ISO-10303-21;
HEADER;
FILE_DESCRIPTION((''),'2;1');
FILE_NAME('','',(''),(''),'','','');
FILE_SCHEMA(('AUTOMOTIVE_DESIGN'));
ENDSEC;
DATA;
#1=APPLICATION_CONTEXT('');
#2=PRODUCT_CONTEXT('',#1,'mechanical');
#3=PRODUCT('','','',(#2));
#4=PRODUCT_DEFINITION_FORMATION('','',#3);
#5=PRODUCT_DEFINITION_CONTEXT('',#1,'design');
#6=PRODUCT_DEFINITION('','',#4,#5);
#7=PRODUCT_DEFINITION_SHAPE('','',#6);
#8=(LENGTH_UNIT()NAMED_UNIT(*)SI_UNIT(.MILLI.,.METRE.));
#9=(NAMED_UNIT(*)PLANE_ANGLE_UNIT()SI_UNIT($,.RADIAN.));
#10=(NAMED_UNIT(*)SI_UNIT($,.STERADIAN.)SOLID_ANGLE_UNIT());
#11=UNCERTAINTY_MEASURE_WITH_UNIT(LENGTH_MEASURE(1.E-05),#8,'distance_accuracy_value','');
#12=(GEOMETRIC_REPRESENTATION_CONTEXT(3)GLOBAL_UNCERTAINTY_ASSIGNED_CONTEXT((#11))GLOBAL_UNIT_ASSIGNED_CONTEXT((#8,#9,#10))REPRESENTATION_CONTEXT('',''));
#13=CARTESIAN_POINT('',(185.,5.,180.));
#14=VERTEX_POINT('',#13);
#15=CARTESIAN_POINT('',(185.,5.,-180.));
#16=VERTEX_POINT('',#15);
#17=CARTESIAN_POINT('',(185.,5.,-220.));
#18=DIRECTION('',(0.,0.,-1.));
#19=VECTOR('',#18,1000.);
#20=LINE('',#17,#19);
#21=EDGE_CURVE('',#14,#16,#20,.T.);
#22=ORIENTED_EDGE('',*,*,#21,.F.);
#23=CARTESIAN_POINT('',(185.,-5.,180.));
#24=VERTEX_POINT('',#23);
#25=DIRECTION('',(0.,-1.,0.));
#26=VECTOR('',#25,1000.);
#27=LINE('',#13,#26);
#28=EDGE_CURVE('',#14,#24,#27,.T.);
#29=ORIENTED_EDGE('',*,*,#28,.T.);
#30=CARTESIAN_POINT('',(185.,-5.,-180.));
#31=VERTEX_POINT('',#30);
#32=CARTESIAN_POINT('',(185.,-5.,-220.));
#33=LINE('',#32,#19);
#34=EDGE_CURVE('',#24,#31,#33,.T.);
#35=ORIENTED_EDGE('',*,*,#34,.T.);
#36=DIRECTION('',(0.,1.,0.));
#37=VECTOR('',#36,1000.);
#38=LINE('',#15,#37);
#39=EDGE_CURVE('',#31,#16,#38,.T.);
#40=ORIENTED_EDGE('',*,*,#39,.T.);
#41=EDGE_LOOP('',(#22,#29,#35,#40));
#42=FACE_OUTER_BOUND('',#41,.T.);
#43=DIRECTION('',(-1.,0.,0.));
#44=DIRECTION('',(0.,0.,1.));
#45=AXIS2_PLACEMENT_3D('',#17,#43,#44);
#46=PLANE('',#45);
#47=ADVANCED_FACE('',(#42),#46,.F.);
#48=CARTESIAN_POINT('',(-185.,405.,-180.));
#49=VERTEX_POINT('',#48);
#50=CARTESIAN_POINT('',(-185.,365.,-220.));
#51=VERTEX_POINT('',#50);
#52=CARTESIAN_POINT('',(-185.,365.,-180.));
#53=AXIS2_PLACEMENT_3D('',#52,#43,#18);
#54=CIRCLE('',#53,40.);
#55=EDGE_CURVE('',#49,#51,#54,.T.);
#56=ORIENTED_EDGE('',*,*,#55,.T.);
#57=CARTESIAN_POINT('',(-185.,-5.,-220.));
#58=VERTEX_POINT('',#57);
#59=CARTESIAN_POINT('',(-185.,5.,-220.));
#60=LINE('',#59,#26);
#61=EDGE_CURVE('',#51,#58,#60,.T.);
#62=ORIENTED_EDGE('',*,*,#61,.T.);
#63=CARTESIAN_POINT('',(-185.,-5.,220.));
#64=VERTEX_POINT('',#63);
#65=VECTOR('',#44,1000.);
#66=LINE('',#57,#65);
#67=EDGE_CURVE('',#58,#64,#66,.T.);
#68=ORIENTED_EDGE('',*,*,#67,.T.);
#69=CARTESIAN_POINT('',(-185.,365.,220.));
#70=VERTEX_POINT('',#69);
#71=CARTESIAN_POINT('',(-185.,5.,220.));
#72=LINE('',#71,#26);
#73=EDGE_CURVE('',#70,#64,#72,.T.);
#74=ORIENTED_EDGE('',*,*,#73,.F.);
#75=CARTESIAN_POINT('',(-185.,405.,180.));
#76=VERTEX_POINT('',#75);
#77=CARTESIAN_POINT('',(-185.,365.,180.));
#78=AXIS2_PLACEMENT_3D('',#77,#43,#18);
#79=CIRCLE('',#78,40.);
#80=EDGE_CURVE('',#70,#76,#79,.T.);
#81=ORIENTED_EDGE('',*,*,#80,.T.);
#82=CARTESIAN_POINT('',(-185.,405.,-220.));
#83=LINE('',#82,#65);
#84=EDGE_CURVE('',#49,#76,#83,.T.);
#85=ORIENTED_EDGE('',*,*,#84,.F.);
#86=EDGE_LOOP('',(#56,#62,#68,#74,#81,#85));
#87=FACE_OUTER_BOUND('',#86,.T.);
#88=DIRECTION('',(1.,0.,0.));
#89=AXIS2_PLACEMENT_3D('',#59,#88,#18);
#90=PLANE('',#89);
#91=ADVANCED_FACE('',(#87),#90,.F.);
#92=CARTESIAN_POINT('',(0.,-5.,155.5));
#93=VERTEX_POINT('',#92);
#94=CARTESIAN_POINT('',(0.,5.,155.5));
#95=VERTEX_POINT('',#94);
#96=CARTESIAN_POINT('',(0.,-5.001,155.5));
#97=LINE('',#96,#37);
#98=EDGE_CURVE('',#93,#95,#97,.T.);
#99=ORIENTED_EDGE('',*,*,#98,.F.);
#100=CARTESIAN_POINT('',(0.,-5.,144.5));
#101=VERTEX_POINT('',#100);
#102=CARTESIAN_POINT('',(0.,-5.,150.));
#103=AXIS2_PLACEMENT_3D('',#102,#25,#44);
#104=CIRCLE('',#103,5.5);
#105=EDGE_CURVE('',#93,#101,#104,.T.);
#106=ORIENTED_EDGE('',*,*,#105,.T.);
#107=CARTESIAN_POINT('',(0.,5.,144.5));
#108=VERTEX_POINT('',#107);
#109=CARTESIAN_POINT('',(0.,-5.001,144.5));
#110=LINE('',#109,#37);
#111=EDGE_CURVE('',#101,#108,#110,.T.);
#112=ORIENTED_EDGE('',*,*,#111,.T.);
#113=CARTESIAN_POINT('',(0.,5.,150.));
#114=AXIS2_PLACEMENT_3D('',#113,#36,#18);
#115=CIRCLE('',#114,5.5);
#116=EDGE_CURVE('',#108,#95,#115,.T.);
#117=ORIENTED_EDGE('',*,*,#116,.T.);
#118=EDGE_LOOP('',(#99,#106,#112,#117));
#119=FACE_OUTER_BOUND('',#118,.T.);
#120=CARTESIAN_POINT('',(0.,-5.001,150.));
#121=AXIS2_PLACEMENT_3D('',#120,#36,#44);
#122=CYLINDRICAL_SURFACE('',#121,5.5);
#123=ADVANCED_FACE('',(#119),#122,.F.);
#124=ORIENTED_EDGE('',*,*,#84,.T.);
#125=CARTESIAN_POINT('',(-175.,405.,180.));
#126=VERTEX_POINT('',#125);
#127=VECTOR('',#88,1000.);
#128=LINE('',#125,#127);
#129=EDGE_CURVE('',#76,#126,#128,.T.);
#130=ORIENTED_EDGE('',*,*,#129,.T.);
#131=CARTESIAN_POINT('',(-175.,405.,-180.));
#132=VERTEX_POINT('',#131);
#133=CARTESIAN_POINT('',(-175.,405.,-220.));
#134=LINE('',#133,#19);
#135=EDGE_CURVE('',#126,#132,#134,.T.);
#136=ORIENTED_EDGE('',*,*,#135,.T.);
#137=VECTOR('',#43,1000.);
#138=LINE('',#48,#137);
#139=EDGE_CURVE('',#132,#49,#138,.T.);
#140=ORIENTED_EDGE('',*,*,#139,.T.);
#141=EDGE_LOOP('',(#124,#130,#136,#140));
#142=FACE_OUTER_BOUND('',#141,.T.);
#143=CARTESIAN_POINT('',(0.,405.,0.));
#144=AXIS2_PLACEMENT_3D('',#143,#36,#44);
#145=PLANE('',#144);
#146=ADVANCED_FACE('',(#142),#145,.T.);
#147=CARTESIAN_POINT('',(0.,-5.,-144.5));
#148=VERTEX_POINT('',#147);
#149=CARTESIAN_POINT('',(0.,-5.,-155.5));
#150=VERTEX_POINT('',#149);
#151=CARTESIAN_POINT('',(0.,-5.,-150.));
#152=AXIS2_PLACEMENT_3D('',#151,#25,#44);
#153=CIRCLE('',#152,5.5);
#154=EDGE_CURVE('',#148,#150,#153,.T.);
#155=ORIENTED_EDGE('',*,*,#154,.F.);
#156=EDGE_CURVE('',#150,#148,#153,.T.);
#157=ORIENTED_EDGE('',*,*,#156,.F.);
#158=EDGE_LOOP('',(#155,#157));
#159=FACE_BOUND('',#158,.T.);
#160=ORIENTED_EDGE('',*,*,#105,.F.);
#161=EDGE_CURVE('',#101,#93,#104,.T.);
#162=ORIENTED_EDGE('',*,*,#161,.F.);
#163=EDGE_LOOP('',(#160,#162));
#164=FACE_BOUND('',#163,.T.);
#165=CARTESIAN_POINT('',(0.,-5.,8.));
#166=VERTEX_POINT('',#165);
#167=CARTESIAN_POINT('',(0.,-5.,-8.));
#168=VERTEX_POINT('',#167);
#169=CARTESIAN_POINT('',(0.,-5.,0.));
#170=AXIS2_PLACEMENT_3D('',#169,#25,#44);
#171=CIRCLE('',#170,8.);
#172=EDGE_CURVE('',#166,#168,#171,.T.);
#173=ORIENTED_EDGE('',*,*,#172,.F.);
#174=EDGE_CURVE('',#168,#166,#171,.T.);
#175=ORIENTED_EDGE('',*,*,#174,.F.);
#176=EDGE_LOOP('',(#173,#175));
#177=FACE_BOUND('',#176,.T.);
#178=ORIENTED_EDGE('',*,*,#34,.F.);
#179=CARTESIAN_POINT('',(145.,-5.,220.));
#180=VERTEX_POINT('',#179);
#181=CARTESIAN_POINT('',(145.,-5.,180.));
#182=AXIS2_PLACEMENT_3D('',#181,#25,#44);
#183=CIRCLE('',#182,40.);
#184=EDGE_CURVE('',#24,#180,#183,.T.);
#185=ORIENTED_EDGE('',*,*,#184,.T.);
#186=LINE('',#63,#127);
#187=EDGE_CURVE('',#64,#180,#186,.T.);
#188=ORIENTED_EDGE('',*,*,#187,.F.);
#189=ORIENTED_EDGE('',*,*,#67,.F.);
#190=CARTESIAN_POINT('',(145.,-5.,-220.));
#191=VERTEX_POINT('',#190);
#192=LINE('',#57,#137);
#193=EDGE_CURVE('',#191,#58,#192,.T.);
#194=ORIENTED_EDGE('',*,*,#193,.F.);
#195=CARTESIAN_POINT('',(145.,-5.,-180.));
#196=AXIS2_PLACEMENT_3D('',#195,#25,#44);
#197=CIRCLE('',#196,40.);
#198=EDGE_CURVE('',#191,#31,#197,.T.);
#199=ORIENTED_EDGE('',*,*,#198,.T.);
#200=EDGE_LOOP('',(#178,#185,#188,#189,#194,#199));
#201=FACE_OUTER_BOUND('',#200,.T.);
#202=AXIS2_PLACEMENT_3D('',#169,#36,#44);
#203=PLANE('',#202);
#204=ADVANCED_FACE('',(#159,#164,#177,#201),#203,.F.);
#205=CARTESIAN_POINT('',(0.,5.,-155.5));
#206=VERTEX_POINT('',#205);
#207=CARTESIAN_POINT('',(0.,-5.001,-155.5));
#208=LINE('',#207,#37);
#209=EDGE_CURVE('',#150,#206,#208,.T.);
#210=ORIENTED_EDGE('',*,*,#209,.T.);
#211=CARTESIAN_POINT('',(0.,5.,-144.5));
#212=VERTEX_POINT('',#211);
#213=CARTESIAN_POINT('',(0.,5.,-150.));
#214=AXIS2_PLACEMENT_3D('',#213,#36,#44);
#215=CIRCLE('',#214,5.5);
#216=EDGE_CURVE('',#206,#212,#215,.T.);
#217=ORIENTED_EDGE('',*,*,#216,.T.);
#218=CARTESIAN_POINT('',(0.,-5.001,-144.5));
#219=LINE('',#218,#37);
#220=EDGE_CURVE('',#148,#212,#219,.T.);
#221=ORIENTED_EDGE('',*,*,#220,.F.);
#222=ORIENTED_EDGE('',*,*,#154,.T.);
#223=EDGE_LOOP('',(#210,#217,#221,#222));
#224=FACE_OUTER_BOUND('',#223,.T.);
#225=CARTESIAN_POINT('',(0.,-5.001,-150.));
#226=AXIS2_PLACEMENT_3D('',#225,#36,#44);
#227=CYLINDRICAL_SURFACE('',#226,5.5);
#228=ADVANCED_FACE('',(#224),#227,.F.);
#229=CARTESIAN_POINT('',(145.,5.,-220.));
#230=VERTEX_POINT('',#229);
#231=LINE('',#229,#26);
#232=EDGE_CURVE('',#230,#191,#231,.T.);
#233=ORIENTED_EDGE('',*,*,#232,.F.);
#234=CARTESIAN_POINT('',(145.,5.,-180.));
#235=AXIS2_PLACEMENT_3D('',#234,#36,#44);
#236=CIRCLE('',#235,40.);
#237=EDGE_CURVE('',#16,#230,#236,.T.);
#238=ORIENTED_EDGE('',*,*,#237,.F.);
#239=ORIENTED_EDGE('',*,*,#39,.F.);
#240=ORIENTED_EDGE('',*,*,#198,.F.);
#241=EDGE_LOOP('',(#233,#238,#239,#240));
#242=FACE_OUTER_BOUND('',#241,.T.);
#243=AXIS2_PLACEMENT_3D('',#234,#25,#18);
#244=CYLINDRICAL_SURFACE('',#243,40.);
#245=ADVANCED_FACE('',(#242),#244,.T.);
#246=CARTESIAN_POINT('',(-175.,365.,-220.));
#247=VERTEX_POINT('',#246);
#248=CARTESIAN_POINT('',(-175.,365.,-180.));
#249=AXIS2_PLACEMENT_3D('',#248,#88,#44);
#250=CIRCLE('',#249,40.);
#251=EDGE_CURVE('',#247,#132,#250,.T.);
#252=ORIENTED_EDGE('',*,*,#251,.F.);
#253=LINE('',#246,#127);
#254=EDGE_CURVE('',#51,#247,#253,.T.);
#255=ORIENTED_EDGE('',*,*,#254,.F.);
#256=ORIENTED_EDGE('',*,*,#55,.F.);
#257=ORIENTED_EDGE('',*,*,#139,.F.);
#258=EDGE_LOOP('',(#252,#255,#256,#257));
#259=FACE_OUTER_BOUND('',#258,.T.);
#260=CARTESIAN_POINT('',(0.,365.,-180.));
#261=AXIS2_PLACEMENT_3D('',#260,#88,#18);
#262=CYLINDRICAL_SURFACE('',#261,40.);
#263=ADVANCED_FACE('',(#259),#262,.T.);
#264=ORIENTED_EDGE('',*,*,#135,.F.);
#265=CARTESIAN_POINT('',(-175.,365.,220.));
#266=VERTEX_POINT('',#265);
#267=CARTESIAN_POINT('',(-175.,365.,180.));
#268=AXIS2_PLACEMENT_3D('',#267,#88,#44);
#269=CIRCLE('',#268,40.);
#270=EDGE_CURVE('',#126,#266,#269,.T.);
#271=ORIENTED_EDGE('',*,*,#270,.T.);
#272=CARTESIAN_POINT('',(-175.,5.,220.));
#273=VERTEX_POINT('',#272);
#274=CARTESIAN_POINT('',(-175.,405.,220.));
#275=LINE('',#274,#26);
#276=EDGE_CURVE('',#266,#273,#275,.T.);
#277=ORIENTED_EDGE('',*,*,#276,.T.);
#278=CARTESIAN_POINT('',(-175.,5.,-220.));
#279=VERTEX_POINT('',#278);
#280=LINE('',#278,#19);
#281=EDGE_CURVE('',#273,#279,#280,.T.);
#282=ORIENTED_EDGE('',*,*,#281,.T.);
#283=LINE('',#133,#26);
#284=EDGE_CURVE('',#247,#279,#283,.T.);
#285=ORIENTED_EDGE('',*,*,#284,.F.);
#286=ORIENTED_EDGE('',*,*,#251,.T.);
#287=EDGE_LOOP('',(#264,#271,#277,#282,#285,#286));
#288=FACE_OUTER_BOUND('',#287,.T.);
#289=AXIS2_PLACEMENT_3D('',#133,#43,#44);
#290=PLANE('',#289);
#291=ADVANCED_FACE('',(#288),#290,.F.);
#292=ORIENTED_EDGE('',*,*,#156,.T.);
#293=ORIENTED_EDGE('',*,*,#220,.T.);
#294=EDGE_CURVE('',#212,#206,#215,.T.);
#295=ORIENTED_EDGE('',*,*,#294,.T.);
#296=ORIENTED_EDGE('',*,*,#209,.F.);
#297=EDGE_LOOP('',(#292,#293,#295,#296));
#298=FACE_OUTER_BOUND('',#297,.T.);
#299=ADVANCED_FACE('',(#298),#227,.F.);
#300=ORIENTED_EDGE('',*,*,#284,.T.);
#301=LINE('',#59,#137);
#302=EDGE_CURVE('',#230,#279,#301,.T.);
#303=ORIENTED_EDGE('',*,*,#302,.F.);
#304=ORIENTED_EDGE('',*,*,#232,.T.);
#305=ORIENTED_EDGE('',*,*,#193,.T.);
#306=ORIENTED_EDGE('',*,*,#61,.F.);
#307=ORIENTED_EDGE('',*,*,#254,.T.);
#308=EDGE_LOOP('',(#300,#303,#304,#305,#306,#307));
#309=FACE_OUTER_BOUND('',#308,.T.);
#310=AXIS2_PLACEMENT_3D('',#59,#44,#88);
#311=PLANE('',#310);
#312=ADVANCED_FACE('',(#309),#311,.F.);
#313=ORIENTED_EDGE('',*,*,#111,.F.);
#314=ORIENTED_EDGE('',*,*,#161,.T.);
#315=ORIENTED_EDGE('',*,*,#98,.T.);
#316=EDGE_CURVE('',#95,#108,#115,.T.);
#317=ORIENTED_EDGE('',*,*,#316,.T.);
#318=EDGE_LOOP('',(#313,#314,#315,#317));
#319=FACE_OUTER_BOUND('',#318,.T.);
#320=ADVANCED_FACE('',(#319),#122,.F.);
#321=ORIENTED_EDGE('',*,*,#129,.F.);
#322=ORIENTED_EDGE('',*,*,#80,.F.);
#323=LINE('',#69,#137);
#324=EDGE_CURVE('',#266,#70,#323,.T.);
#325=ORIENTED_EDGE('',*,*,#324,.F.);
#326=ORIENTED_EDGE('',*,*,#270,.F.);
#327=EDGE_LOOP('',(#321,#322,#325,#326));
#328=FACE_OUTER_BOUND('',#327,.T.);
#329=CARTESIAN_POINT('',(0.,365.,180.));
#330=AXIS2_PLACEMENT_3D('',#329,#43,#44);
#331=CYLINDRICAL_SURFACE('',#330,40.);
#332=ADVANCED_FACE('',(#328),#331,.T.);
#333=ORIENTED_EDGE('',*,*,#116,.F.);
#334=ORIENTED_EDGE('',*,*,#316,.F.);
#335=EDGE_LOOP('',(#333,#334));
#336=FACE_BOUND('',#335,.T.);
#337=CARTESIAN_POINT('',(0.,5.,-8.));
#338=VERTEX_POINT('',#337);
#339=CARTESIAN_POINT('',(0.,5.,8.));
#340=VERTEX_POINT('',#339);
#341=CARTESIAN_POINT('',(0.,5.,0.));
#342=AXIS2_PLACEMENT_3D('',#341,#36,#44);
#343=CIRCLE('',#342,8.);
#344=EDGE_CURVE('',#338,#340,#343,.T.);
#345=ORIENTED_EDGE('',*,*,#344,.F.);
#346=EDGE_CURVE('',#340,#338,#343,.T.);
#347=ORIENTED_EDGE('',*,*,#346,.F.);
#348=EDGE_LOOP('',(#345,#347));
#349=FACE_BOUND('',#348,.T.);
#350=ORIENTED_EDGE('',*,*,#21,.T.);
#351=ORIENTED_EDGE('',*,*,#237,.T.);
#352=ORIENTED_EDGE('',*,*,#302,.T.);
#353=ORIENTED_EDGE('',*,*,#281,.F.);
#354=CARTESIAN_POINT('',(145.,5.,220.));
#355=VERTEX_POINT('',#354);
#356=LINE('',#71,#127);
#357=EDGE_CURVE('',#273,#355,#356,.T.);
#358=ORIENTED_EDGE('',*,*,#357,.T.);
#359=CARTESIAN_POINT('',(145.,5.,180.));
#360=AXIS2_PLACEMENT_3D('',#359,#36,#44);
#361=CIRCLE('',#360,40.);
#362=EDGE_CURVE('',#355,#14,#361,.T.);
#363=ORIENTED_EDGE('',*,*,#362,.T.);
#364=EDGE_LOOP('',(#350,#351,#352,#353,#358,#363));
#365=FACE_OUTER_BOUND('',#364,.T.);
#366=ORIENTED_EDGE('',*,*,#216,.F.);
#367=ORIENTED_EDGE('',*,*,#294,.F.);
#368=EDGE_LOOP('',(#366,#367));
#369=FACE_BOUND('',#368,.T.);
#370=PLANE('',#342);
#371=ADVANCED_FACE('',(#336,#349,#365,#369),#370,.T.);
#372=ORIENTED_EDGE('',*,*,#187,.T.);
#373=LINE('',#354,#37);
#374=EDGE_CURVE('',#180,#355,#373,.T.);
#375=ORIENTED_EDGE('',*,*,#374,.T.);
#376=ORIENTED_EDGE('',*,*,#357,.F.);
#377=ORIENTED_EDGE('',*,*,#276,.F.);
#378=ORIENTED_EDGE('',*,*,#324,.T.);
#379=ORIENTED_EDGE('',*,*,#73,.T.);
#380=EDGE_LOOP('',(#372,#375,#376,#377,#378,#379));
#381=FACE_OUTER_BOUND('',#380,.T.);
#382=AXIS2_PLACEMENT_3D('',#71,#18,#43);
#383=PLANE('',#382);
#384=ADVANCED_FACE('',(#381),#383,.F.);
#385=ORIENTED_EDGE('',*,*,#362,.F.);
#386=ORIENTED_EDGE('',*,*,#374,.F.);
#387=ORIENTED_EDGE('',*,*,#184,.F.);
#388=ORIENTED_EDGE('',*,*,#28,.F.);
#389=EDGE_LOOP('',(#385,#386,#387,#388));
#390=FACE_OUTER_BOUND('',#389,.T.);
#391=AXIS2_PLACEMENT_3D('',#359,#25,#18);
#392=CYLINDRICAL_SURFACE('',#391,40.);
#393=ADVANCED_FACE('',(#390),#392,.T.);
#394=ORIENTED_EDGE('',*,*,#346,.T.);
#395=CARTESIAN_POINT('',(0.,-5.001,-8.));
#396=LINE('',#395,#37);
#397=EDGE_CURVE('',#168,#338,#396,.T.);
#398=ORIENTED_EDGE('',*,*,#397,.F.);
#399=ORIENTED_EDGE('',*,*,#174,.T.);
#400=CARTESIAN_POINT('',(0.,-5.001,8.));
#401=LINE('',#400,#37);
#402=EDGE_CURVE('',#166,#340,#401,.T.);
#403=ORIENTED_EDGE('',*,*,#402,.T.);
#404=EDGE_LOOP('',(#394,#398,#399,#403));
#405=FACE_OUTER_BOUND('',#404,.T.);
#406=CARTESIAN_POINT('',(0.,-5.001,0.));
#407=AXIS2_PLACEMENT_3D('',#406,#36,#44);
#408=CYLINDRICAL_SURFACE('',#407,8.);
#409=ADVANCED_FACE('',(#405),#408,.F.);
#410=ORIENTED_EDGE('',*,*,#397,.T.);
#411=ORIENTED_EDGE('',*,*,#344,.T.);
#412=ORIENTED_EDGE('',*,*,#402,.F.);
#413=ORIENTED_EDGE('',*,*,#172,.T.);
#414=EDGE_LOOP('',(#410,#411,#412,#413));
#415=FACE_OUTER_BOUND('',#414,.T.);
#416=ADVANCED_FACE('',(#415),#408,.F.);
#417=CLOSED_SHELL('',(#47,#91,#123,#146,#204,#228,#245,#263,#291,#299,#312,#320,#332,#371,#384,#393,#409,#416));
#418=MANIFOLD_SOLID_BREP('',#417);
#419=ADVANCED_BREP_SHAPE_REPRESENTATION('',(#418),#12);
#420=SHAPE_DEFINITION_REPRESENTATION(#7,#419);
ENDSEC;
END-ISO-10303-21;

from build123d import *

# Parameters (mm, degrees)
SKETCH_1_W          = 370
SKETCH_1_H          = 440
EXTRUDE_1_DEPTH     = 5
CUT_EXTRUDE_1_REACH = 289.62
SKETCH_2_R          = 8
SKETCH_2_R_2        = 5.5
SKETCH_3_W          = 10
SKETCH_3_H          = 440
EXTRUDE_2_DEPTH     = 400
FILLET_1_R          = 40


with BuildPart() as part:
    # 草图1 → 凸台-拉伸1 (new, symmetric)
    with BuildSketch(Plane(origin=(0, 0, 0), x_dir=(1, 0, 0), z_dir=(0, 1, 0))):
        Rectangle(SKETCH_1_W, SKETCH_1_H)
    extrude(amount=EXTRUDE_1_DEPTH, both=True)

    # 草图2 → 切除-拉伸1 (cut, up to next)
    with BuildSketch(Plane(origin=(0, 5, 0), x_dir=(1, 0, 0), z_dir=(0, 1, 0)), mode=Mode.PRIVATE) as cut_extrude_1_sk1:
        with Locations(Location((0, 0, 0), (0, 0, 270))):
            Circle(SKETCH_2_R)
    cut_extrude_1_tool1 = extrude(cut_extrude_1_sk1.sketch, amount=-CUT_EXTRUDE_1_REACH, mode=Mode.PRIVATE) & part.part
    # 草图2 → 切除-拉伸1 (cut, up to next)
    with BuildSketch(Plane(origin=(0, 5, 0), x_dir=(1, 0, 0), z_dir=(0, 1, 0)), mode=Mode.PRIVATE) as cut_extrude_1_sk2:
        with Locations(Location((0, 150, 0), (0, 0, 270))):
            Circle(SKETCH_2_R_2)
    cut_extrude_1_tool2 = extrude(cut_extrude_1_sk2.sketch, amount=-CUT_EXTRUDE_1_REACH, mode=Mode.PRIVATE) & part.part
    # 草图2 → 切除-拉伸1 (cut, up to next)
    with BuildSketch(Plane(origin=(0, 5, 0), x_dir=(1, 0, 0), z_dir=(0, 1, 0)), mode=Mode.PRIVATE) as cut_extrude_1_sk3:
        with Locations(Location((0, -150, 0), (0, 0, 270))):
            Circle(SKETCH_2_R_2)
    cut_extrude_1_tool3 = extrude(cut_extrude_1_sk3.sketch, amount=-CUT_EXTRUDE_1_REACH, mode=Mode.PRIVATE) & part.part
    add(cut_extrude_1_tool1.solids().sort_by_distance((0, 5, 0))[0], mode=Mode.SUBTRACT)
    add(cut_extrude_1_tool2.solids().sort_by_distance((0, 5, -150))[0], mode=Mode.SUBTRACT)
    add(cut_extrude_1_tool3.solids().sort_by_distance((0, 5, 150))[0], mode=Mode.SUBTRACT)

    # 草图3 → 凸台-拉伸2 (add)
    with BuildSketch(Plane(origin=(0, 5, 0), x_dir=(1, 0, 0), z_dir=(0, 1, 0))):
        with Locations((-180, 0)):
            Rectangle(SKETCH_3_W, SKETCH_3_H)
    extrude(amount=EXTRUDE_2_DEPTH)

    # 圆角1
    fillet_1_edges = [part.edges().sort_by_distance(p)[0] for p in [
        (-180, 405, 220),
        (-180, 405, -220),
        (185, 0, 220),
        (185, 0, -220),
    ]]
    fillet(fillet_1_edges, radius=FILLET_1_R)


solid = part.part
